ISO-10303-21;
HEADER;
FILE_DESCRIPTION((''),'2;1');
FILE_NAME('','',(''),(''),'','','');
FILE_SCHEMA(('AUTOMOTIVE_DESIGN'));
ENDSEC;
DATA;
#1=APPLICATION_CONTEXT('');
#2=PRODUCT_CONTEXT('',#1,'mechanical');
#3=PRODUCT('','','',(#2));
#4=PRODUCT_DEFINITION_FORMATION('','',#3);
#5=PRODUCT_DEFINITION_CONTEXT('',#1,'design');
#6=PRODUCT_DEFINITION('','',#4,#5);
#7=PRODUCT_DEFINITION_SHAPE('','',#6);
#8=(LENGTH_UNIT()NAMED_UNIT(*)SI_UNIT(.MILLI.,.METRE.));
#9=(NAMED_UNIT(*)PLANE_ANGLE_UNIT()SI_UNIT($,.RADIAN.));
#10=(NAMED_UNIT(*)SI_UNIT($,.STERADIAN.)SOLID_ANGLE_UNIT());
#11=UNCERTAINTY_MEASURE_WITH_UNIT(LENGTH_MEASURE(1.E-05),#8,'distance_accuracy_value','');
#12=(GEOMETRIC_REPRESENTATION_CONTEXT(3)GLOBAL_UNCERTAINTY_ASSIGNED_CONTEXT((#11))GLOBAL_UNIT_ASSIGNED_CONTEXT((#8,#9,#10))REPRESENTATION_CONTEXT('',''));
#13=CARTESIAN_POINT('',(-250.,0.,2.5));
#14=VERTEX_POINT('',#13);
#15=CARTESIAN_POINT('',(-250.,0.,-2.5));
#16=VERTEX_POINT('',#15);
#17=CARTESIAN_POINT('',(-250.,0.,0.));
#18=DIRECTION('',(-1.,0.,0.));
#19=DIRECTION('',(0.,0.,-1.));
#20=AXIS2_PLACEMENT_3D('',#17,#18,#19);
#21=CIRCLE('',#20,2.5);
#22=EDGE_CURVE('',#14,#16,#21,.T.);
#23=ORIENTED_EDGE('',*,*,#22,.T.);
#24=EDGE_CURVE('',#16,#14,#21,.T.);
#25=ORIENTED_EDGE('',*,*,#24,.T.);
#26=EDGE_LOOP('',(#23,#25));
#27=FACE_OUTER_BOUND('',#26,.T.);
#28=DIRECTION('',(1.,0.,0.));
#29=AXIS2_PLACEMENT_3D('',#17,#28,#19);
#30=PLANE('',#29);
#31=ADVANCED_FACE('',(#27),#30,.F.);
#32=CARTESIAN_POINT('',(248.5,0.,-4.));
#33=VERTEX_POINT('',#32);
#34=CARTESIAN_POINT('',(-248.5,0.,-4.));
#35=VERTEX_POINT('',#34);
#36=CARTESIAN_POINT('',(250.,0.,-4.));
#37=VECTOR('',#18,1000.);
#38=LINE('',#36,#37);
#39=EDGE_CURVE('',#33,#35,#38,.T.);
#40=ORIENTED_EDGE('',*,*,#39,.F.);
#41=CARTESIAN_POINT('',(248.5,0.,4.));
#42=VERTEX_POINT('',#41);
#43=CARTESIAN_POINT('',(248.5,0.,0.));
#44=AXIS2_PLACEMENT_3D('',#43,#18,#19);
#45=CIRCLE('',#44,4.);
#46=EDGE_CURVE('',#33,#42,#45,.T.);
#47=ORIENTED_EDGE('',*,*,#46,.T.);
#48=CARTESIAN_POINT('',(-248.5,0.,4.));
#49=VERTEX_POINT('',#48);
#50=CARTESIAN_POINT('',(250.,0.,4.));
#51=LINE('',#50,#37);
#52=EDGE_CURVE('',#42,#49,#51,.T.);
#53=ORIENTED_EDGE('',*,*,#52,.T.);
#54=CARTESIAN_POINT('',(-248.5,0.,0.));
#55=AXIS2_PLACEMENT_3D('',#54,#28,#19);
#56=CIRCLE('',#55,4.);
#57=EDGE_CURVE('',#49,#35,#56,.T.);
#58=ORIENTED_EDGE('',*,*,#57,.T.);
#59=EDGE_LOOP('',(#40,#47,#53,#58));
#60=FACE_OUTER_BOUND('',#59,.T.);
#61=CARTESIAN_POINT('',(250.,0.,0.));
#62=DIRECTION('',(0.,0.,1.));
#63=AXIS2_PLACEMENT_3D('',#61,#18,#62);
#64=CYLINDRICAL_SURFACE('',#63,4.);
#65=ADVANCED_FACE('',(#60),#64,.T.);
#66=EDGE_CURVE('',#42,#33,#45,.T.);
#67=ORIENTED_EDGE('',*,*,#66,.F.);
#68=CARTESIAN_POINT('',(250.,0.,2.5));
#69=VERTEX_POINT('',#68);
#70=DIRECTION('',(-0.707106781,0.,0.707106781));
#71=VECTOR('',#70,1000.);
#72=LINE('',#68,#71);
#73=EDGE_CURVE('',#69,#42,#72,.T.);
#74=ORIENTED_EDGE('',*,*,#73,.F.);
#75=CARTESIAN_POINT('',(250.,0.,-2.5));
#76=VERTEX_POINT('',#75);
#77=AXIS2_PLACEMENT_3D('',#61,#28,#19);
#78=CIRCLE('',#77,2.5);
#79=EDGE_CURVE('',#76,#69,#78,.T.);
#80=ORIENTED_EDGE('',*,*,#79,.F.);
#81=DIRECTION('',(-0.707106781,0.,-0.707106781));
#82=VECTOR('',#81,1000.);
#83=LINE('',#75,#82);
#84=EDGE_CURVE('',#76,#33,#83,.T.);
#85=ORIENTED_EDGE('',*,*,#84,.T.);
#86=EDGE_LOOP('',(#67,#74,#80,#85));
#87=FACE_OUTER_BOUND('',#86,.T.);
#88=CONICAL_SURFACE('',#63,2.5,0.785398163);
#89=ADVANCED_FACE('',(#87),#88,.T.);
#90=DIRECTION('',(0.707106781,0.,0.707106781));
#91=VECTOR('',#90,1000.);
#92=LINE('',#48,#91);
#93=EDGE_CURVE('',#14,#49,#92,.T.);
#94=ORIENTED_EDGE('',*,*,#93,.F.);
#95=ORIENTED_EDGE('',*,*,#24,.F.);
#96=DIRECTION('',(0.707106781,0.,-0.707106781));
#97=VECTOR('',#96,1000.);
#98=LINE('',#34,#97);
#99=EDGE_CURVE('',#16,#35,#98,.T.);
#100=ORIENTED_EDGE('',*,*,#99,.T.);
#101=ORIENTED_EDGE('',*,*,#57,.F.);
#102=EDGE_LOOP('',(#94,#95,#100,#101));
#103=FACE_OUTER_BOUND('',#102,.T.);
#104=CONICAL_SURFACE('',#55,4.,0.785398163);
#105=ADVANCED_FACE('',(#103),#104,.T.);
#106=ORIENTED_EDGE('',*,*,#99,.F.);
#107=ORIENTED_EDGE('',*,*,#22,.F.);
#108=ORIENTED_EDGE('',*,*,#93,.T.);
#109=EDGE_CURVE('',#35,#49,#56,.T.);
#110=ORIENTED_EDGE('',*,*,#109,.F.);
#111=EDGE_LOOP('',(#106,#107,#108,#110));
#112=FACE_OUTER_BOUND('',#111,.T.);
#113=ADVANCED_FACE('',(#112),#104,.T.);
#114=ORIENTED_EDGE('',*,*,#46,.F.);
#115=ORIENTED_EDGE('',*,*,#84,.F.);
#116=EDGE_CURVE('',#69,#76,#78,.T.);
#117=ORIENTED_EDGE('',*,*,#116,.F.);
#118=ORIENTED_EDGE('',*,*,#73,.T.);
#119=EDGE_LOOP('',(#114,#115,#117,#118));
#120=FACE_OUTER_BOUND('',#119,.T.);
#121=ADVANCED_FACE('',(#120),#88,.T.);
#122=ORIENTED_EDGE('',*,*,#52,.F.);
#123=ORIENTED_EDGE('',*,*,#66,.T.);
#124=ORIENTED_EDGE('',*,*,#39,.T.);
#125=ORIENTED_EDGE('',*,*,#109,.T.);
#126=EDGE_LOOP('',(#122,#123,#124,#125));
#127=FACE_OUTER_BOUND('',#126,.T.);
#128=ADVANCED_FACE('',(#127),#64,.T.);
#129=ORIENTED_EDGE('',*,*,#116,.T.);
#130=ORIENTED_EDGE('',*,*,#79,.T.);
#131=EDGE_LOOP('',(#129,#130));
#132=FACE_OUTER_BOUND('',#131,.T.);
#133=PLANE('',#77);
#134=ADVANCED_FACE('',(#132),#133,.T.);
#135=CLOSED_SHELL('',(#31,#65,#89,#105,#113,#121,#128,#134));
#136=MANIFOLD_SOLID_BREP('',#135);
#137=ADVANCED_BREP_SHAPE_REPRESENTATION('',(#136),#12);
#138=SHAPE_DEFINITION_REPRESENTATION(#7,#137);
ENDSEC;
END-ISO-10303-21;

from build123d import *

# Parameters (mm, degrees)
SKETCH1_R           = 4
BOSS_EXTRUDE1_DEPTH = 250
CHAMFER1_SIZE       = 1.5


with BuildPart() as part:
    # Sketch1 → Boss-Extrude1 (new, symmetric)
    with BuildSketch(Plane(origin=(0, 0, 0), x_dir=(0, 0, -1), z_dir=(1, 0, 0))):
        Circle(SKETCH1_R)
    extrude(amount=BOSS_EXTRUDE1_DEPTH, both=True)

    # Chamfer1
    chamfer1_edges = [part.edges().sort_by_distance(p)[0] for p in [
        (-250, 0, 4),
        (250, 0, 4),
    ]]
    chamfer(chamfer1_edges, length=CHAMFER1_SIZE)


solid = part.part
